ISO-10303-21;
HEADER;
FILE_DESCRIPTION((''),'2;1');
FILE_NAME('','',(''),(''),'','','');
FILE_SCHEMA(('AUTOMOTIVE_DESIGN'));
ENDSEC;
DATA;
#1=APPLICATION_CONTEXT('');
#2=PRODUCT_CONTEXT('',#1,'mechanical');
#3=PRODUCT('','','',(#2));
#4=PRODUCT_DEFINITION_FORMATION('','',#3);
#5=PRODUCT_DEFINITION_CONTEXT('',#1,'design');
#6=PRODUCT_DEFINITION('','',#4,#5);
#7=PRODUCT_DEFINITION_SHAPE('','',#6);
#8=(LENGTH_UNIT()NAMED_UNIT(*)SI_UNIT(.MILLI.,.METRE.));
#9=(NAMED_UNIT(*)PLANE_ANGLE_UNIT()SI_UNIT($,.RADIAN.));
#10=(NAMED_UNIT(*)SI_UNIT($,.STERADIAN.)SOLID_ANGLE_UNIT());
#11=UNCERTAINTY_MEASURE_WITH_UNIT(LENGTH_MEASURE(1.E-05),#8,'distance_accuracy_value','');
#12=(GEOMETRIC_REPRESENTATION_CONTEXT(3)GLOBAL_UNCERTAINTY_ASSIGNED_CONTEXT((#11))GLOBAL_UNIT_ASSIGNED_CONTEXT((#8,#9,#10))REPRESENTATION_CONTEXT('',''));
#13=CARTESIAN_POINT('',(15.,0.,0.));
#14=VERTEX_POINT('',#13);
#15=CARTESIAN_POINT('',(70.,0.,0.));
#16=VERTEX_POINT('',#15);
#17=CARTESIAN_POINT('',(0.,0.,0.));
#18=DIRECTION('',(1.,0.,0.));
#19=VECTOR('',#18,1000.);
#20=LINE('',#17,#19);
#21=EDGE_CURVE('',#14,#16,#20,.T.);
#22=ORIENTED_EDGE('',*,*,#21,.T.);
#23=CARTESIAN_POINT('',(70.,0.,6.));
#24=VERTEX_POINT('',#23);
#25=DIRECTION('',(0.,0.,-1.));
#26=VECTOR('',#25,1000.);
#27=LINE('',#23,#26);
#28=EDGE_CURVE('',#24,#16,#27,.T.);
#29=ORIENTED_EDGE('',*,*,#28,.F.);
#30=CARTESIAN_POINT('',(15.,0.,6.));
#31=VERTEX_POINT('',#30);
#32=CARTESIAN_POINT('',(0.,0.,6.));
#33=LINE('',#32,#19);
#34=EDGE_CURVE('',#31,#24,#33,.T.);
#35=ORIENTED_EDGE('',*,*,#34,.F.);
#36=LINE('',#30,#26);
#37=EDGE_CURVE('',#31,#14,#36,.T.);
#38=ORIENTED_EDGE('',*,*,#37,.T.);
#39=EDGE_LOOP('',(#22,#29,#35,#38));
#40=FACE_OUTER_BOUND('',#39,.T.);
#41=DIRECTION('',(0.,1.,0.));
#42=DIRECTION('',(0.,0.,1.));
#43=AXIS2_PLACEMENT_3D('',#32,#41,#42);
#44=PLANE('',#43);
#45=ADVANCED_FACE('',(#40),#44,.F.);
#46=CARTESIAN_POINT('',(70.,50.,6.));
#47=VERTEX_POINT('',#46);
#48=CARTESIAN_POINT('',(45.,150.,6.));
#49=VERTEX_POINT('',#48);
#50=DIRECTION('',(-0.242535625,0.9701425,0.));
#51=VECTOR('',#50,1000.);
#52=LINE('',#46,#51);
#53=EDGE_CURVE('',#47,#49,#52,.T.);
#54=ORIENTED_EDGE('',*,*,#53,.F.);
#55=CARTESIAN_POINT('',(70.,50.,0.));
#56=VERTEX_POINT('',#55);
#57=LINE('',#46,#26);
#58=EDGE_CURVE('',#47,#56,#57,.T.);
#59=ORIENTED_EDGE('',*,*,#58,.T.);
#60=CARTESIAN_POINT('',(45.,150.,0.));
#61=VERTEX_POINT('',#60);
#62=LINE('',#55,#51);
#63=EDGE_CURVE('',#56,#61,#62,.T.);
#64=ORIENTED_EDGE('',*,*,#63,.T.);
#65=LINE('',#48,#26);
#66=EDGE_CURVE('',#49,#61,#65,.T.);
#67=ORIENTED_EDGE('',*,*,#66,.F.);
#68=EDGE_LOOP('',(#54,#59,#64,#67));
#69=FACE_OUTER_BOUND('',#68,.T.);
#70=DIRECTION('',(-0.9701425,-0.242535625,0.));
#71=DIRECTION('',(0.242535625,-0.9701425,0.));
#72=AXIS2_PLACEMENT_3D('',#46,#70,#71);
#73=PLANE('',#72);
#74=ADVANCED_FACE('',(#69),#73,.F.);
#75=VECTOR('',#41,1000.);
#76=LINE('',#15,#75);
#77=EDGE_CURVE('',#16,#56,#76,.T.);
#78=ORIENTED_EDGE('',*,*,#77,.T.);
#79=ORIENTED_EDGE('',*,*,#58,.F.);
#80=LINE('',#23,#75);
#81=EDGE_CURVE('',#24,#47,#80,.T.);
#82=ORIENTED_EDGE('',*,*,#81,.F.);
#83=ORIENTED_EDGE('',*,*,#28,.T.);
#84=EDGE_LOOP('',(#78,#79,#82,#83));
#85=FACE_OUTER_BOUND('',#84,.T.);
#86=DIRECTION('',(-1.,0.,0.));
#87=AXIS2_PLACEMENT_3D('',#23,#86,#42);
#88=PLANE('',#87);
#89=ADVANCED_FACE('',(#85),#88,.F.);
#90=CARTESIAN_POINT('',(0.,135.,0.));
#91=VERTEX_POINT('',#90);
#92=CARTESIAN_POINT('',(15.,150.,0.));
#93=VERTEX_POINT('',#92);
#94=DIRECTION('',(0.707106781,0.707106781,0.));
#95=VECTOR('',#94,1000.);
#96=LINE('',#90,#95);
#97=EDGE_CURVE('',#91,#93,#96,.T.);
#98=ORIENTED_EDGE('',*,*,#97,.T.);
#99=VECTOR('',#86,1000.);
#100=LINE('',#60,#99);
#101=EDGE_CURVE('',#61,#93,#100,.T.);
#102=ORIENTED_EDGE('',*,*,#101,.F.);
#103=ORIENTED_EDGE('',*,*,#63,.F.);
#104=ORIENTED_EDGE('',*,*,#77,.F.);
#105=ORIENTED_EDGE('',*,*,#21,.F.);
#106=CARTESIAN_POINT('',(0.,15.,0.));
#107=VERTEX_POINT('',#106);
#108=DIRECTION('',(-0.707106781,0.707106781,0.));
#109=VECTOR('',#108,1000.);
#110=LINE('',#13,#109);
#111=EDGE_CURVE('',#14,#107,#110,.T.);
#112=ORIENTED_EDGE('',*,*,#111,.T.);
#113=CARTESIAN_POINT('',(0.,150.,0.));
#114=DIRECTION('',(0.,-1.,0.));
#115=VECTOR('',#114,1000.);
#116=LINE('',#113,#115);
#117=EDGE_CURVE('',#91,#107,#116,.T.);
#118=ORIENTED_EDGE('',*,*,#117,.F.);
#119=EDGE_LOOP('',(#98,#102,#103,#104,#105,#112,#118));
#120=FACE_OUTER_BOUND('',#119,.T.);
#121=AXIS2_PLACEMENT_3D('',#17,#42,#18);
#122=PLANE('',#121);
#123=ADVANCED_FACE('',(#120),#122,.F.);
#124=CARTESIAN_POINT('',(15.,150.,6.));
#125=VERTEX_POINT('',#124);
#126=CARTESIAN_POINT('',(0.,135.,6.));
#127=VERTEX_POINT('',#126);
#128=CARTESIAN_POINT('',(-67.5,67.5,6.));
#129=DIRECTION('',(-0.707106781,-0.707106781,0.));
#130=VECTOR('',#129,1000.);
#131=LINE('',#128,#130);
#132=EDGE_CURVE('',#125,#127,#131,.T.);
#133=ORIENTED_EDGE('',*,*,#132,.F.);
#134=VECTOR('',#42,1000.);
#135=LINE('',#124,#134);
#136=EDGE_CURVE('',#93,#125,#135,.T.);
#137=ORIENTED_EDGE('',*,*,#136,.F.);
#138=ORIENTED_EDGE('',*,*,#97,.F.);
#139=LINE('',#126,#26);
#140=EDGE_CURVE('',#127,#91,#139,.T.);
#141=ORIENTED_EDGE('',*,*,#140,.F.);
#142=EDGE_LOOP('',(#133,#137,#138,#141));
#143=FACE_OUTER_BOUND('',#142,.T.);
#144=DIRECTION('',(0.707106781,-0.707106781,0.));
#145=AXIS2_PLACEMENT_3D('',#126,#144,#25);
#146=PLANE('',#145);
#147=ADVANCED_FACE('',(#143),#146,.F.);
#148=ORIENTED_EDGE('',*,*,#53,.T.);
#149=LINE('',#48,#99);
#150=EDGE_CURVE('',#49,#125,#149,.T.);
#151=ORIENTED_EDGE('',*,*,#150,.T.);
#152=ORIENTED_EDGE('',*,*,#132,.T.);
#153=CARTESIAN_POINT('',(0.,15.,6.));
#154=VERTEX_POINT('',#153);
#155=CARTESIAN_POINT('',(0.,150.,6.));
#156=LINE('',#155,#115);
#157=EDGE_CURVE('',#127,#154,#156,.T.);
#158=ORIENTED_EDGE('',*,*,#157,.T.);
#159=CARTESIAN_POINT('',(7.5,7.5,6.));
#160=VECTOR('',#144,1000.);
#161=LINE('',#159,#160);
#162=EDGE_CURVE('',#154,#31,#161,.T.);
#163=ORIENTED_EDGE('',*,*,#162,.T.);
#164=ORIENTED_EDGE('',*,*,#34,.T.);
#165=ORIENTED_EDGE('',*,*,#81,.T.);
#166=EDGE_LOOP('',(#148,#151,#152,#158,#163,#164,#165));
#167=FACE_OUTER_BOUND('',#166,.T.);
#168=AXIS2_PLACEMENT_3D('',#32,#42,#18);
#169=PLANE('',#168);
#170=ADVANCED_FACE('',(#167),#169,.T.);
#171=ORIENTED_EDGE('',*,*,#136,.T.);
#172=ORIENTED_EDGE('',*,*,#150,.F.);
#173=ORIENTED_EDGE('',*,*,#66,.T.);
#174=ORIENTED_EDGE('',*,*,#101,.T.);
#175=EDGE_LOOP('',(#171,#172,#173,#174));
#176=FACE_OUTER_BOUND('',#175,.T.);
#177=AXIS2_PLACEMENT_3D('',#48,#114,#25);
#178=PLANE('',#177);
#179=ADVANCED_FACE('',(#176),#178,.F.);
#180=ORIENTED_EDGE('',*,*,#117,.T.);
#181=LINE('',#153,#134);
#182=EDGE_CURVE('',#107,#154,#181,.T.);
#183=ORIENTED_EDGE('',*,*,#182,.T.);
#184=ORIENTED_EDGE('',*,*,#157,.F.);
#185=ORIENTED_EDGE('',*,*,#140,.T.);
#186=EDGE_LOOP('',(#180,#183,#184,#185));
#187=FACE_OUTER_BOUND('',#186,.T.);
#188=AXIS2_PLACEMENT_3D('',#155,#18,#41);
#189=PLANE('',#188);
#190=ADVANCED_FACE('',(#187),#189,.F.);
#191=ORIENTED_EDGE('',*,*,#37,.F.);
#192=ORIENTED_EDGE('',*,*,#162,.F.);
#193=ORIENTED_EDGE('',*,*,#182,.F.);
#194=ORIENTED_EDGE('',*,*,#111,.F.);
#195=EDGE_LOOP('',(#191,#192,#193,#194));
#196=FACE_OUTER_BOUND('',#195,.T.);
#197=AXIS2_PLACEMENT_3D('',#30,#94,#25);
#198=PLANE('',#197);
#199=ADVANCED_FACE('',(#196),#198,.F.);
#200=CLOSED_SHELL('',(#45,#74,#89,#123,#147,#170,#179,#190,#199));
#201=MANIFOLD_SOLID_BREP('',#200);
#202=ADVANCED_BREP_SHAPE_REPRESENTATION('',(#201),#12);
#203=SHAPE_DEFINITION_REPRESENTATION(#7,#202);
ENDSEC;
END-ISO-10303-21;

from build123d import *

# Parameters (mm, degrees)
BOSS_EXTRUDE1_DEPTH = 6
CHAMFER1_SIZE       = 15


with BuildPart() as part:
    # Sketch1 → Boss-Extrude1 (new body)
    with BuildSketch(Plane.XY):
        Polygon((0, 150), (0, 0), (70, 0), (70, 50), (45, 150), align=None)
    extrude(amount=BOSS_EXTRUDE1_DEPTH)

    # Chamfer1
    chamfer1_edges = [part.edges().sort_by_distance(p)[0] for p in [
        (0, 0, 3),
        (0, 150, 3),
    ]]
    chamfer(chamfer1_edges, length=CHAMFER1_SIZE)


solid = part.part
